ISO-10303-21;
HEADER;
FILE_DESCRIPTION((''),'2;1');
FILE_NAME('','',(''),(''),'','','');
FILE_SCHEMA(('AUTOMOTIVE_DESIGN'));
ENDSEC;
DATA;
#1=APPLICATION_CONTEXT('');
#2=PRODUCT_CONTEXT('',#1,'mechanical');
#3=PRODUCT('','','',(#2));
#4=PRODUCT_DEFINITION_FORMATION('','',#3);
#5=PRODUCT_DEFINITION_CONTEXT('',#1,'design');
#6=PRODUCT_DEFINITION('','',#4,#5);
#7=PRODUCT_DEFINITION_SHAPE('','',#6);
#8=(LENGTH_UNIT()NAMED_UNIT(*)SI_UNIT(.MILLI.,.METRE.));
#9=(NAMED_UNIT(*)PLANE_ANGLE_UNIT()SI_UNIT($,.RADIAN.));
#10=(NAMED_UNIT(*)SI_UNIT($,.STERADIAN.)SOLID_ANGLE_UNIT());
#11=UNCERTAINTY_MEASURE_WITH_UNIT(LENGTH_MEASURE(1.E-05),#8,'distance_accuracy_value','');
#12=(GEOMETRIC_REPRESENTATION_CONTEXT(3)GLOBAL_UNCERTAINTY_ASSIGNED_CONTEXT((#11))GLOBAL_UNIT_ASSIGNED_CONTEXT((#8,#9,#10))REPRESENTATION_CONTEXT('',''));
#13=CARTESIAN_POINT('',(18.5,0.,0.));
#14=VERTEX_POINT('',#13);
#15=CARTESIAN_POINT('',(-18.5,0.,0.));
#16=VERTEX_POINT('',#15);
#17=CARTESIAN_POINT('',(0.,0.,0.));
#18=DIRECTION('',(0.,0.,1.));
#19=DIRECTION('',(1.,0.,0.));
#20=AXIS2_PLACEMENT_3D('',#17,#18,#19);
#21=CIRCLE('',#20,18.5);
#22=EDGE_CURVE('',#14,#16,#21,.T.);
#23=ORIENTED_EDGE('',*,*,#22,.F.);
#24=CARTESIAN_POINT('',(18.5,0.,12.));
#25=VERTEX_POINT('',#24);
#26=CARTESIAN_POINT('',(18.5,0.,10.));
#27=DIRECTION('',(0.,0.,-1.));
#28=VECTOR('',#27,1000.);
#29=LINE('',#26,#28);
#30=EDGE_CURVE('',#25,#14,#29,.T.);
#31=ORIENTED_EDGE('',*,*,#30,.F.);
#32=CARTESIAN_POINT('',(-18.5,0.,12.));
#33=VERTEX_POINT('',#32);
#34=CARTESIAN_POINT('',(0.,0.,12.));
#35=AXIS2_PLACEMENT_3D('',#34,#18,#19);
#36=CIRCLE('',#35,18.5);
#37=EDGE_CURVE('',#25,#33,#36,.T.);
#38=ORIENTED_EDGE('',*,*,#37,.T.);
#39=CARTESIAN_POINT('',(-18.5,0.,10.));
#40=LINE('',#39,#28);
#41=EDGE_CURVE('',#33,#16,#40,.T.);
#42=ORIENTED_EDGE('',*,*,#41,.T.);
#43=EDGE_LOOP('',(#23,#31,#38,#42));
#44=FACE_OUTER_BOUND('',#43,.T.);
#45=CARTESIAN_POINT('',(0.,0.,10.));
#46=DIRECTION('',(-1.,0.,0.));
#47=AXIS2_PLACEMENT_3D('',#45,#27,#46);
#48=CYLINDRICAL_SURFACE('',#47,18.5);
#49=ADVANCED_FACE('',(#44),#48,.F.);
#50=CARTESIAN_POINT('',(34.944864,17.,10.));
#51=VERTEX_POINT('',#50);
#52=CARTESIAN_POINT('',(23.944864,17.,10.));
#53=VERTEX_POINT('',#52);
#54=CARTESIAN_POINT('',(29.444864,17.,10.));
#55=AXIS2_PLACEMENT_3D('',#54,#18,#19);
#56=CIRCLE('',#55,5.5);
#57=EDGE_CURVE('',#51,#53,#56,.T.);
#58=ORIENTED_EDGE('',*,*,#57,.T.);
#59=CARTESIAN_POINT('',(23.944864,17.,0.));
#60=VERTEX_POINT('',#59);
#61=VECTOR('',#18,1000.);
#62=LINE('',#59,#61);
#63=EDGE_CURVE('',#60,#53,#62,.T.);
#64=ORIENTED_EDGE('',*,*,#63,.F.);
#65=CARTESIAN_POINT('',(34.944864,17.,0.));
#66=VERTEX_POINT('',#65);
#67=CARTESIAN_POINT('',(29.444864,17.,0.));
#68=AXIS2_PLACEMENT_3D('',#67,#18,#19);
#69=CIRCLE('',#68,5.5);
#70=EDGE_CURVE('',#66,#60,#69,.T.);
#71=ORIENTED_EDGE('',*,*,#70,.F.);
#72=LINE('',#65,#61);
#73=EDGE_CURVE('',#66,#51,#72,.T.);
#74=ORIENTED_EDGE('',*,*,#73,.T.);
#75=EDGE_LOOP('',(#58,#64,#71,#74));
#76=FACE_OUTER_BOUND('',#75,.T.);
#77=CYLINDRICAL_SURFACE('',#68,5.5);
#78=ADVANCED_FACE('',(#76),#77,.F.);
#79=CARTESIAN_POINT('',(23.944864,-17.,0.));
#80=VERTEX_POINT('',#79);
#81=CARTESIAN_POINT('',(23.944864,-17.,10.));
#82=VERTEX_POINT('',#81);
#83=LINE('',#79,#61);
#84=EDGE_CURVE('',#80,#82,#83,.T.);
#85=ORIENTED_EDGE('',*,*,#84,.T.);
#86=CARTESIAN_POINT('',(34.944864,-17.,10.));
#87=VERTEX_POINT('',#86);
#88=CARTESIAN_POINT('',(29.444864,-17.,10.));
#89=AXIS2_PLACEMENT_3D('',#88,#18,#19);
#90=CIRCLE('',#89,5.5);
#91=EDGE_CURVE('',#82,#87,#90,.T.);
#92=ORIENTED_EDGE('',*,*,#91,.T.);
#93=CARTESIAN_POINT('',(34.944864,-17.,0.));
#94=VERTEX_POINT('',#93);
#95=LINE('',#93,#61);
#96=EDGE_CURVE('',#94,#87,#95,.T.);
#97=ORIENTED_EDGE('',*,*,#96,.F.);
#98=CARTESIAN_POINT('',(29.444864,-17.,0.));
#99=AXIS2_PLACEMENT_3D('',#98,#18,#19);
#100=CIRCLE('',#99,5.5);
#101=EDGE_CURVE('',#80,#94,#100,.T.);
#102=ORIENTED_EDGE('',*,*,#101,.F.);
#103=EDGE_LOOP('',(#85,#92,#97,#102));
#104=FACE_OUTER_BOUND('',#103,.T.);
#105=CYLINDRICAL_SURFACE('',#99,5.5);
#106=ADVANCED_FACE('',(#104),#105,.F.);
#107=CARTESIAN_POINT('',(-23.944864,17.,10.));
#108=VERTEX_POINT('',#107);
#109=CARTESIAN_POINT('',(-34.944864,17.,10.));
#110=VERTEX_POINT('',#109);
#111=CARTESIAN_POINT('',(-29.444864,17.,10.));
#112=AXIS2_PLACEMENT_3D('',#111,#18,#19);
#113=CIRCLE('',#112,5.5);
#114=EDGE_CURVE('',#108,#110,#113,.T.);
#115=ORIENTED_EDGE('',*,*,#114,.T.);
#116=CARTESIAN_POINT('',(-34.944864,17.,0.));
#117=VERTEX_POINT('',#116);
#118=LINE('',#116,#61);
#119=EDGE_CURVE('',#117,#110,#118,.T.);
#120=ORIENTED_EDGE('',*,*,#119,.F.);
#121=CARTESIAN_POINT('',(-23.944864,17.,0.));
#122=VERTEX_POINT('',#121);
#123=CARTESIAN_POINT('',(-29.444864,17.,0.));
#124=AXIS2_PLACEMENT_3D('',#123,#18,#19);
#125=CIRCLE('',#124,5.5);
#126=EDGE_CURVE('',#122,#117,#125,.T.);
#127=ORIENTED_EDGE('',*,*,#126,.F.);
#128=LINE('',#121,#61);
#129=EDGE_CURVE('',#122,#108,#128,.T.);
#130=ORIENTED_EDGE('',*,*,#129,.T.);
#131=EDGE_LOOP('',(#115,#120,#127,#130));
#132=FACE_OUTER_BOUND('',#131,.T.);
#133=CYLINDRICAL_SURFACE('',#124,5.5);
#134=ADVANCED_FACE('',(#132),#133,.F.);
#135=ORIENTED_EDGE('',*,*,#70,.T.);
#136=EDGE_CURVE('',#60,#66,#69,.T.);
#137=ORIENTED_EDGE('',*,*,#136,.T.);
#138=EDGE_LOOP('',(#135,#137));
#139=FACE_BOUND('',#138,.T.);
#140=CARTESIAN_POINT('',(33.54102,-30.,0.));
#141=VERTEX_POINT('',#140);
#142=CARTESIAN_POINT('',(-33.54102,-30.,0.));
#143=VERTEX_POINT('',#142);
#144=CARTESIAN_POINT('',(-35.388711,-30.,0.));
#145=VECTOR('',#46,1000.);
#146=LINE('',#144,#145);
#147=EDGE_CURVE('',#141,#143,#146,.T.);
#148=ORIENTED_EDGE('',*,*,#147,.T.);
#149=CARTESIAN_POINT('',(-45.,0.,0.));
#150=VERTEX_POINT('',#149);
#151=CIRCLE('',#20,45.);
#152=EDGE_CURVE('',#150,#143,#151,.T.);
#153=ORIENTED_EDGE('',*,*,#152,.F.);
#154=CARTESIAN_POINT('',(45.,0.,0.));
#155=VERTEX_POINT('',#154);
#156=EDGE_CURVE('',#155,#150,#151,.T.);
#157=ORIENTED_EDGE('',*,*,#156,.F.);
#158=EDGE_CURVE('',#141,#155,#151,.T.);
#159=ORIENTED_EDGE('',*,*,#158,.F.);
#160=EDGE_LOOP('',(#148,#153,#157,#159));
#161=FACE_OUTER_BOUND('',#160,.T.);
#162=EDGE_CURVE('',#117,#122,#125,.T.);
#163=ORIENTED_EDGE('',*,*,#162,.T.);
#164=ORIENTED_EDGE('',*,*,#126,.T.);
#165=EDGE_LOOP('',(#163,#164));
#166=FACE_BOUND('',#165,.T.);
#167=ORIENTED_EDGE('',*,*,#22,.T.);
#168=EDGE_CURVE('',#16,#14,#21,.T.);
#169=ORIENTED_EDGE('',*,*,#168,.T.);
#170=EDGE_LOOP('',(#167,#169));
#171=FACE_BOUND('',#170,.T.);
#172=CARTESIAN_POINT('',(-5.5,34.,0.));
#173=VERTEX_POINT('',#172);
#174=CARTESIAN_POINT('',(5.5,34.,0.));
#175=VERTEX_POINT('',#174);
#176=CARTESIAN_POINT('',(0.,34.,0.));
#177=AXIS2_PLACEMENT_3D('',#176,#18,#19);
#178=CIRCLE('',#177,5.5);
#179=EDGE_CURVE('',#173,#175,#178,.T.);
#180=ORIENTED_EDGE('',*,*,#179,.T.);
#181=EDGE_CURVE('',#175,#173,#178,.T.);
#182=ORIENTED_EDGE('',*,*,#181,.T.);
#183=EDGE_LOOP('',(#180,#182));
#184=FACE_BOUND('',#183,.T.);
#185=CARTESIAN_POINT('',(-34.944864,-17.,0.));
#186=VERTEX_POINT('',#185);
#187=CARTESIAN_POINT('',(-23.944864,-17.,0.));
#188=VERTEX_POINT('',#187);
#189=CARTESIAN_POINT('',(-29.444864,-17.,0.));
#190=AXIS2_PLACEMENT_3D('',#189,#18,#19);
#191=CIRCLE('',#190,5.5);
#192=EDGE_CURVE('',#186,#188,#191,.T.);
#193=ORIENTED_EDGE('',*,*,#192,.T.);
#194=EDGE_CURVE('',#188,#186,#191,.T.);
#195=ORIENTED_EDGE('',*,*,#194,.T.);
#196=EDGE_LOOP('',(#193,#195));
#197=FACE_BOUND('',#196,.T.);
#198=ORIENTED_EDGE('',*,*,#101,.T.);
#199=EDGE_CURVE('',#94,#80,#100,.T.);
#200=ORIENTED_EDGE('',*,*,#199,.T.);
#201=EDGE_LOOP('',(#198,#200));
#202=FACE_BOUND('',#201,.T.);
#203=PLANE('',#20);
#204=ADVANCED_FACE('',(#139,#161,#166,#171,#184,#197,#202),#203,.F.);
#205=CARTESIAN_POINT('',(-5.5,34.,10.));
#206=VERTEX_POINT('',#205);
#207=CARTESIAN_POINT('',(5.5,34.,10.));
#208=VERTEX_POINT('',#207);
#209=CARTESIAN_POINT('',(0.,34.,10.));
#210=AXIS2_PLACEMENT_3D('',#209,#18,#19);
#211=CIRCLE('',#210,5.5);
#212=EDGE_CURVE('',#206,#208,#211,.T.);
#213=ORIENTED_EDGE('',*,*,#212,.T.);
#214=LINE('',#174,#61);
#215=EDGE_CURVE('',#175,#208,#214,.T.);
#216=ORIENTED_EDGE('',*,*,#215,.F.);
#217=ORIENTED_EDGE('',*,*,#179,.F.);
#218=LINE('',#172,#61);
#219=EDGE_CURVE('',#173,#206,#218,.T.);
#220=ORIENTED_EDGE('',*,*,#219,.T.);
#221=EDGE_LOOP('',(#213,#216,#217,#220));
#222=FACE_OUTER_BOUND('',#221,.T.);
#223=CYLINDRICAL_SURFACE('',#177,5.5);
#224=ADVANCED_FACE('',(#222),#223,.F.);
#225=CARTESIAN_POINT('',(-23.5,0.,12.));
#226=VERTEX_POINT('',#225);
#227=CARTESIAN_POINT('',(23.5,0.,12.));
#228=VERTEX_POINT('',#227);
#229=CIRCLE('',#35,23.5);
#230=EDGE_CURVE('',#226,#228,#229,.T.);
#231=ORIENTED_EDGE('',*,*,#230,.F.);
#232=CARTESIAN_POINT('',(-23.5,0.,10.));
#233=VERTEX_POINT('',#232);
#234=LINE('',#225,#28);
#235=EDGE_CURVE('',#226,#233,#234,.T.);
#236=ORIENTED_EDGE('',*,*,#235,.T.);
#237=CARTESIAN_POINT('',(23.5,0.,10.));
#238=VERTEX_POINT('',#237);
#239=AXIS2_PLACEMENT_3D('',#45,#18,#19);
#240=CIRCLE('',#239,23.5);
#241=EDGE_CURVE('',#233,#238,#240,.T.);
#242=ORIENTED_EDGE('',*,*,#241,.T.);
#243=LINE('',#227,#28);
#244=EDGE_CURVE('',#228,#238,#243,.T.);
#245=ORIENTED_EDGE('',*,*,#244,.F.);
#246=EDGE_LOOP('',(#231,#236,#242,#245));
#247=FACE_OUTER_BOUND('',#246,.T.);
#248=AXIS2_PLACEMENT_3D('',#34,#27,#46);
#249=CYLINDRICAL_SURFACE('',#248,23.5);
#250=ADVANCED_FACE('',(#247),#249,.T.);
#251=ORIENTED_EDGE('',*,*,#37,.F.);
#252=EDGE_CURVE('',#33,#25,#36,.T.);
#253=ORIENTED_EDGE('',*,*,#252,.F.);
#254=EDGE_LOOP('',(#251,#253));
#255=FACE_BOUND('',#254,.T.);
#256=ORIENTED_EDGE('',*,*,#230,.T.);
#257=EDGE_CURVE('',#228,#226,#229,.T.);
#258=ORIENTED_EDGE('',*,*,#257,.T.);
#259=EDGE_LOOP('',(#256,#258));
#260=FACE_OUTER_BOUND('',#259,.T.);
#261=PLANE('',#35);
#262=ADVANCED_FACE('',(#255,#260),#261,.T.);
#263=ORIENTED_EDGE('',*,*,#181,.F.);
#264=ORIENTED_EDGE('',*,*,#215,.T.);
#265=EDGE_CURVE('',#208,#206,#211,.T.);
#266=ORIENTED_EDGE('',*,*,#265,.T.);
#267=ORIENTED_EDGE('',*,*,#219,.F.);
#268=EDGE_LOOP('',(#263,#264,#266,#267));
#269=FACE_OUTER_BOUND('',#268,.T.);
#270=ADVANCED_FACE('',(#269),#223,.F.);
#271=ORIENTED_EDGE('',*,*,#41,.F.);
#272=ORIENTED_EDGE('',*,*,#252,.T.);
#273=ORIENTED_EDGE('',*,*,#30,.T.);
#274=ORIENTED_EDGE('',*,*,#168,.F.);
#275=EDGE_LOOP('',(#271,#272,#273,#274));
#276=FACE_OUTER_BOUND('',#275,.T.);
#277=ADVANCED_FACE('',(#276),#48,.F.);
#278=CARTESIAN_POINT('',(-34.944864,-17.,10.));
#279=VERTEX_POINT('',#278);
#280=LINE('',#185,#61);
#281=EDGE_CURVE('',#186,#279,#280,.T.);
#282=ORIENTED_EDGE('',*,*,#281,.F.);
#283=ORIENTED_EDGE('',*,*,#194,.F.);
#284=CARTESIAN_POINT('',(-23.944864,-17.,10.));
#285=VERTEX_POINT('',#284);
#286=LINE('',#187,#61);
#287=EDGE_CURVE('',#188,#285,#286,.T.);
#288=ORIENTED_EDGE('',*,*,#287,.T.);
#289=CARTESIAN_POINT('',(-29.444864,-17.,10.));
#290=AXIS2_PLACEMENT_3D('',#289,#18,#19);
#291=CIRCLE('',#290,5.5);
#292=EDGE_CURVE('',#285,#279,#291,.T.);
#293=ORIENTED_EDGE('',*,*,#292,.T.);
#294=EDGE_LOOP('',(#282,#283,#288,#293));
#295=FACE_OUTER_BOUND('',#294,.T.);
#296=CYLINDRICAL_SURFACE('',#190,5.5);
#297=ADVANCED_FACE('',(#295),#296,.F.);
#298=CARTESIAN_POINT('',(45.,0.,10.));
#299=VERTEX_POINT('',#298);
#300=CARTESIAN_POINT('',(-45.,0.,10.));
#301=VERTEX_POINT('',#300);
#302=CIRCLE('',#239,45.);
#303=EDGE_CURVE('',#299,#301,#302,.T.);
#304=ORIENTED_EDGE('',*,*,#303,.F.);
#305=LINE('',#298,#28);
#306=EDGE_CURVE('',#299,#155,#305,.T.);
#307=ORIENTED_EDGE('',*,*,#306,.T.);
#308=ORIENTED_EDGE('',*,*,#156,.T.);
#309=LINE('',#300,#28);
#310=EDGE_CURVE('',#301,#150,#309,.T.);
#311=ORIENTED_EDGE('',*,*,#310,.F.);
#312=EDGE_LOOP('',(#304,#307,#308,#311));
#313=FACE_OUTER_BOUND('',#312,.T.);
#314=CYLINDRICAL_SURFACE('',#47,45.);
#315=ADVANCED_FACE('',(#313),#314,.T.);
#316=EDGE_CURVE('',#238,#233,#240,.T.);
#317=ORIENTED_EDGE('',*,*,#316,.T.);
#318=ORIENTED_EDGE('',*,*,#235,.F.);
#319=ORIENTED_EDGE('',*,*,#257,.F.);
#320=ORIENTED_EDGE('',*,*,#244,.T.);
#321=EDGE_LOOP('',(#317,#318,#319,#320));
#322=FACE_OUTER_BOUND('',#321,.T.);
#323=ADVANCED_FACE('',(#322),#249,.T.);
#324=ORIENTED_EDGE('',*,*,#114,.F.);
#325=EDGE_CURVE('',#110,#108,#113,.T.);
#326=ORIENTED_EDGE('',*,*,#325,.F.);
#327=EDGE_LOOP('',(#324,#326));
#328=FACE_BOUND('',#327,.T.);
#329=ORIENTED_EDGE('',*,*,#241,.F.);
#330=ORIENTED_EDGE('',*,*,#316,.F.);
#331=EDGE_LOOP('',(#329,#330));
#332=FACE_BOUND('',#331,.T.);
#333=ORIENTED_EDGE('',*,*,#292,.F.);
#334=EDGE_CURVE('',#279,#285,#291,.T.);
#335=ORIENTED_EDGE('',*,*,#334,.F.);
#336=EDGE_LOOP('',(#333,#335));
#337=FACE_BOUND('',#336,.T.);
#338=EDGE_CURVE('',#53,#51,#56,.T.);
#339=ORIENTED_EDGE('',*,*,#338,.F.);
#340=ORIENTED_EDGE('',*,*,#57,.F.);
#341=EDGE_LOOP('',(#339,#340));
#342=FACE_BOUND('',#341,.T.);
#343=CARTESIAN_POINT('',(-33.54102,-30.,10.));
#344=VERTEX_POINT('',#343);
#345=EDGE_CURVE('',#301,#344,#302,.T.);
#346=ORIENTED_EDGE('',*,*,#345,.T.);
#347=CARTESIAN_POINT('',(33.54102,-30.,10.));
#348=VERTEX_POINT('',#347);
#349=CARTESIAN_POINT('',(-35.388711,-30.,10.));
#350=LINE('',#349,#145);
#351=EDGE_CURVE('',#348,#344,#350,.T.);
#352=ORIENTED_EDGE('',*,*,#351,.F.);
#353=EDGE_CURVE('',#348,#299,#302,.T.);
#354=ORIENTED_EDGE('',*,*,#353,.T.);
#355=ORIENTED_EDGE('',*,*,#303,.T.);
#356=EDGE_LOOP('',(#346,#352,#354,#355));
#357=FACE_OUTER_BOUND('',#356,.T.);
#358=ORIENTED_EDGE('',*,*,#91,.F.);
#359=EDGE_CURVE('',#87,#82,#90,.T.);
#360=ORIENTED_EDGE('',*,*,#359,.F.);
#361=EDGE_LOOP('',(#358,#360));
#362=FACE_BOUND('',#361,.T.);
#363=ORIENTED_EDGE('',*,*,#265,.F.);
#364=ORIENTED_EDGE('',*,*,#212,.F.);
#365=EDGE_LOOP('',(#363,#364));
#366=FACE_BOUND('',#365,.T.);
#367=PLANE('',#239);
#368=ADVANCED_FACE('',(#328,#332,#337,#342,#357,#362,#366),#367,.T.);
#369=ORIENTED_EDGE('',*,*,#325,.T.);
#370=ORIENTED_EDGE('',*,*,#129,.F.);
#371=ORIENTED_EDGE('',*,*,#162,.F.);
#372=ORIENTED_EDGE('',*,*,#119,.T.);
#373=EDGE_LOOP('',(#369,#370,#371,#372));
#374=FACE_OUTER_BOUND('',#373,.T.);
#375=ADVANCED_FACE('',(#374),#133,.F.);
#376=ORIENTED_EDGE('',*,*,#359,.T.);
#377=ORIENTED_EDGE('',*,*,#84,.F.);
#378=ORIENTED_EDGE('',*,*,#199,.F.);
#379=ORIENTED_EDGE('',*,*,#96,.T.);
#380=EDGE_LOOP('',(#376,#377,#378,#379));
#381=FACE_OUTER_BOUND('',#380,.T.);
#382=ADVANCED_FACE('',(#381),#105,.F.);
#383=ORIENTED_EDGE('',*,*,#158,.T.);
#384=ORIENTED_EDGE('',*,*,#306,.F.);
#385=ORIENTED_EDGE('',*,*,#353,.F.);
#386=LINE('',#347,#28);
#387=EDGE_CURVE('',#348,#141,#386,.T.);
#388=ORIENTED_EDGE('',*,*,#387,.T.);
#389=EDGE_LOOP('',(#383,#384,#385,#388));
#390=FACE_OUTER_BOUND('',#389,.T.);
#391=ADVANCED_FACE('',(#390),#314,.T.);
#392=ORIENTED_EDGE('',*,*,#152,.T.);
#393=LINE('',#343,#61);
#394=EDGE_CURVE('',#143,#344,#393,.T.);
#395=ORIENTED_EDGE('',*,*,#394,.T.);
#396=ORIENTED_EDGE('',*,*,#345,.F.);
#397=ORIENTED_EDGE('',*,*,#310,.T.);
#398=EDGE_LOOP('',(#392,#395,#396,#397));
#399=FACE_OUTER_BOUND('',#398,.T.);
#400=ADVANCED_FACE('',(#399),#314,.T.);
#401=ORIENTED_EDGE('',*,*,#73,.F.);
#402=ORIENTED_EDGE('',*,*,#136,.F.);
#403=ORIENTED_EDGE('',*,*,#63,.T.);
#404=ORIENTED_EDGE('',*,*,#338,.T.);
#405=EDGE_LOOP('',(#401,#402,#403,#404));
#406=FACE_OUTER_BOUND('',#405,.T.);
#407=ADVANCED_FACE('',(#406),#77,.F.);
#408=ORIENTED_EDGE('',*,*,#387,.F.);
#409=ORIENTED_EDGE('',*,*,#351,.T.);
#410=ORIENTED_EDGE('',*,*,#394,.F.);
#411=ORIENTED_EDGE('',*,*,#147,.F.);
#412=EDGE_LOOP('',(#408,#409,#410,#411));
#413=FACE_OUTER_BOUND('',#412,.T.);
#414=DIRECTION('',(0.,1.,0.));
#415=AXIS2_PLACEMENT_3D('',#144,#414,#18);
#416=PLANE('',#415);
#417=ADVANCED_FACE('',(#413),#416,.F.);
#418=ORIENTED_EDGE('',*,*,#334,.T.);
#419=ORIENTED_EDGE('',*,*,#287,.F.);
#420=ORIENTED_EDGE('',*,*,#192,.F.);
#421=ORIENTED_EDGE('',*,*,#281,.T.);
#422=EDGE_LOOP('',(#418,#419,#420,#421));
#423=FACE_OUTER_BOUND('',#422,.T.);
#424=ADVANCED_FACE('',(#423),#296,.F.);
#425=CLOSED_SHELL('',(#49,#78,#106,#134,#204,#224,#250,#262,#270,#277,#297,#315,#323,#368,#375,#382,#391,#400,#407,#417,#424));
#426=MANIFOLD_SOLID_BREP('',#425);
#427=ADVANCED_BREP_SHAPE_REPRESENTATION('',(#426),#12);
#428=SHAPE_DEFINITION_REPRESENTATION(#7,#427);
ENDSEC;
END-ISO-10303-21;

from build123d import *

# Parameters (mm, degrees)
SKETCH_1_R          = 45
SKETCH_1_R_2        = 18.5
EXTRUDE_1_DEPTH     = 10
SKETCH_2_R          = 23.5
SKETCH_2_R_2        = 18.5
EXTRUDE_2_DEPTH     = 2
SKETCH_3_R          = 5.5
CUT_EXTRUDE_1_DEPTH = 65.420493634
CUT_EXTRUDE_2_DEPTH = 65.420493634


with BuildPart() as part:
    # 草图1 → 拉伸1 (new body)
    with BuildSketch(Plane.XY):
        Circle(SKETCH_1_R)
        Circle(SKETCH_1_R_2, mode=Mode.SUBTRACT)
    extrude(amount=EXTRUDE_1_DEPTH)

    # 草图2 → 拉伸2 (add)
    with BuildSketch(Plane.XY.offset(10)):
        Circle(SKETCH_2_R)
        Circle(SKETCH_2_R_2, mode=Mode.SUBTRACT)
    extrude(amount=EXTRUDE_2_DEPTH)

    # 草图3 → 切除-拉伸1 (cut, through all)
    with BuildSketch(Plane.XY.offset(10)):
        with Locations((0, 34)):
            Circle(SKETCH_3_R)
        with Locations((-29.444863729, 17)):
            Circle(SKETCH_3_R)
        with Locations((-29.444863729, -17)):
            Circle(SKETCH_3_R)
        with Locations((29.444863729, 17)):
            Circle(SKETCH_3_R)
        with Locations((29.444863729, -17)):
            Circle(SKETCH_3_R)
    extrude(amount=-CUT_EXTRUDE_1_DEPTH, mode=Mode.SUBTRACT)

    # 草图4 → 切除-拉伸2 (cut, through all)
    with BuildSketch(Plane.XY.offset(10)):
        with BuildLine():
            Line((-35.388711425, -30), (35.388711425, -30))
            ThreePointArc((35.388711425, -30), (0, -46.393543692), (-35.388711425, -30))
        make_face()
    extrude(amount=-CUT_EXTRUDE_2_DEPTH, mode=Mode.SUBTRACT)


solid = part.part
